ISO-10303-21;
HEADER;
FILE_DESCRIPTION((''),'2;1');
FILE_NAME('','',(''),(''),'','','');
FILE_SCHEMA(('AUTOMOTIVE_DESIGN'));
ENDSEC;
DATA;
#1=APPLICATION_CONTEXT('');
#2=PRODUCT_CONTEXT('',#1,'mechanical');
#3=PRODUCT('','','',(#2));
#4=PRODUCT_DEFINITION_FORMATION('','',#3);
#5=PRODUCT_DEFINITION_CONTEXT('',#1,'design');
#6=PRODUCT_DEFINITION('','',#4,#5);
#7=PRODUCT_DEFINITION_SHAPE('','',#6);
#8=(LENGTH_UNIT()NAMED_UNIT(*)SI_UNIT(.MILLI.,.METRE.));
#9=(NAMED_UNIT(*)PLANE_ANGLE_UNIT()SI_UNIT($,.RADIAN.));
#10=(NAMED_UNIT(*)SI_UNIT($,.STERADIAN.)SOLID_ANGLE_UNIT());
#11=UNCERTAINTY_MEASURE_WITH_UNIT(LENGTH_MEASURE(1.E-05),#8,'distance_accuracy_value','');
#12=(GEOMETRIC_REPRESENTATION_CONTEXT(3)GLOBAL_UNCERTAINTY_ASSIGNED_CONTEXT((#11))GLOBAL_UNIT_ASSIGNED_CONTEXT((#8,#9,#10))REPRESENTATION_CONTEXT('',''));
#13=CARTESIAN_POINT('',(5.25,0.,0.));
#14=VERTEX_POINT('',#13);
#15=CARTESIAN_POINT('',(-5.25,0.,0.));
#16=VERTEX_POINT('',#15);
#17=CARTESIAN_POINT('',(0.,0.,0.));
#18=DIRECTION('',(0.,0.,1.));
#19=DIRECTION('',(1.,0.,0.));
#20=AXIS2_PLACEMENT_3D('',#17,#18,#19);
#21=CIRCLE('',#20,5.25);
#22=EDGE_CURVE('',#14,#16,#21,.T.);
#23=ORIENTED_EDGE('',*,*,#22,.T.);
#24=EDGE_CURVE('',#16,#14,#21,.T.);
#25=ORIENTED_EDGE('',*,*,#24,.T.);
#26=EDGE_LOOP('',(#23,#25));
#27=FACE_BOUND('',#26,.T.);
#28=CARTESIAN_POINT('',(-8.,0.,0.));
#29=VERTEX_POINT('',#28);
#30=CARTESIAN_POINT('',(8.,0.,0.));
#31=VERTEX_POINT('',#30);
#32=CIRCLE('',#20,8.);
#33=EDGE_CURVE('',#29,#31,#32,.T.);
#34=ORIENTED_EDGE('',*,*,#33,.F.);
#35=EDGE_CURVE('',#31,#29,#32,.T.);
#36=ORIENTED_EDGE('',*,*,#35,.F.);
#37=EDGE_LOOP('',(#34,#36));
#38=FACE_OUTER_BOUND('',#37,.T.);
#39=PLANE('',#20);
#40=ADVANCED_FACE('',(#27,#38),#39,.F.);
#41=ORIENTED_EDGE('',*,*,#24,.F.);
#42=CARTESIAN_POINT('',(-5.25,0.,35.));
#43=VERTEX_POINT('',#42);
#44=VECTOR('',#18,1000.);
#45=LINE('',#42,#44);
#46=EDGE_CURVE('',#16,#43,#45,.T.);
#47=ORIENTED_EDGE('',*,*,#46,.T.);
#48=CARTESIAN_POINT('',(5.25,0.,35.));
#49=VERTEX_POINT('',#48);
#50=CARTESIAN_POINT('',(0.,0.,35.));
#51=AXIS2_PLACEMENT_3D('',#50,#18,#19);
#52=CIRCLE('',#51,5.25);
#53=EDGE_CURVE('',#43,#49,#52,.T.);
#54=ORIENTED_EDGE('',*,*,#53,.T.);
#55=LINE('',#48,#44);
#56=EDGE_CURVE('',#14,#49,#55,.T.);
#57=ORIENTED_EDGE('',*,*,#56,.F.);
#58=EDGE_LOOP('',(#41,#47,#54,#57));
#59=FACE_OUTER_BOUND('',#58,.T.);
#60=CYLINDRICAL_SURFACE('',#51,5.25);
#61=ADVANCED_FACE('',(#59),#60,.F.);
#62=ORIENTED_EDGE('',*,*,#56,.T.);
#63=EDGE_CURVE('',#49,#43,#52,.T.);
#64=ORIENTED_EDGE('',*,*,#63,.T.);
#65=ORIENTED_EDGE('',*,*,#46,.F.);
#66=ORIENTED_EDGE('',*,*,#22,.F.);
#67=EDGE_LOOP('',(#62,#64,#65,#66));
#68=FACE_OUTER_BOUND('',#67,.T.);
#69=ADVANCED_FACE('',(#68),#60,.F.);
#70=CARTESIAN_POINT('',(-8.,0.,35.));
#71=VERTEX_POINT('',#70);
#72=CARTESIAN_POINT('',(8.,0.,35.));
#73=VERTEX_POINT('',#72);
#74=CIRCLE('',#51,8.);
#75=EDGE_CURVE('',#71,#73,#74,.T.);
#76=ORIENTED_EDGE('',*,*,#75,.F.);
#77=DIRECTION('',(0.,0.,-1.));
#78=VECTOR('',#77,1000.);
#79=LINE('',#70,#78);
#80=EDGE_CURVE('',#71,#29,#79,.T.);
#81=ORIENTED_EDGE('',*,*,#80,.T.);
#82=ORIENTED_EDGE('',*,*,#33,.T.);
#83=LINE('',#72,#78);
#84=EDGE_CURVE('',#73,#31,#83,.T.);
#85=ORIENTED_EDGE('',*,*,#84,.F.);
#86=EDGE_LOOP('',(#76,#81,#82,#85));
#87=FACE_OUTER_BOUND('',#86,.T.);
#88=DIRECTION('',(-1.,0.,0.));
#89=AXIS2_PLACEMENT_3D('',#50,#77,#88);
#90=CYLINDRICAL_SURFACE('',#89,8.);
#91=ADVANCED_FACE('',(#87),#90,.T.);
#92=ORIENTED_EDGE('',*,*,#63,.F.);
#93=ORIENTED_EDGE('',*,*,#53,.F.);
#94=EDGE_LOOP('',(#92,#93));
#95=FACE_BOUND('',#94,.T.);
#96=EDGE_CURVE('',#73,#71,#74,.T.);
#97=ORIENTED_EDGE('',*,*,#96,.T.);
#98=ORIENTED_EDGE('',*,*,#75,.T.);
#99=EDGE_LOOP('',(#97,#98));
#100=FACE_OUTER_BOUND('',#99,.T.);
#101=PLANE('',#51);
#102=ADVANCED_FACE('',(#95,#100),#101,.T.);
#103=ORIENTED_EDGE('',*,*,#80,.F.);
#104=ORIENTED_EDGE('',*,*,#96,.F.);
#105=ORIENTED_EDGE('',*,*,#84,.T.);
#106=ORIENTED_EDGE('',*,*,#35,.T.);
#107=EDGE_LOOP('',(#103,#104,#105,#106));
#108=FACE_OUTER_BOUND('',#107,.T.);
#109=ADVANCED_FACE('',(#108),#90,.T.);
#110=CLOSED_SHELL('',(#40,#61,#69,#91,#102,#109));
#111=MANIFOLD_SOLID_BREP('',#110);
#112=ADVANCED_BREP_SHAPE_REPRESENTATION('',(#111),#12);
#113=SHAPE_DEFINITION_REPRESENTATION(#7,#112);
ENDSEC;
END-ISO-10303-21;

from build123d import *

# Parameters (mm, degrees)
SKETCH1_R                   = 8
BOSS_EXTRUDE1_DEPTH         = 35
M12X1_25_TAPPED_HOLE1_D     = 10.5
M12X1_25_TAPPED_HOLE1_DEPTH = 35
M12X1_25_TAPPED_HOLE1_TIP   = 3.15451825


with BuildPart() as part:
    # Sketch1 → Boss-Extrude1 (new body)
    with BuildSketch(Plane.XY):
        Circle(SKETCH1_R)
    extrude(amount=BOSS_EXTRUDE1_DEPTH)

    # M12x1.25 Tapped Hole1
    with Locations(Plane.XY.offset(35)):
        with Locations((0, 0)):
            Hole(M12X1_25_TAPPED_HOLE1_D / 2, depth=M12X1_25_TAPPED_HOLE1_DEPTH)
            with Locations((0, 0, -(M12X1_25_TAPPED_HOLE1_DEPTH + M12X1_25_TAPPED_HOLE1_TIP / 2))):  # 118° drill point
                Cone(0, M12X1_25_TAPPED_HOLE1_D / 2, M12X1_25_TAPPED_HOLE1_TIP, mode=Mode.SUBTRACT)


solid = part.part
